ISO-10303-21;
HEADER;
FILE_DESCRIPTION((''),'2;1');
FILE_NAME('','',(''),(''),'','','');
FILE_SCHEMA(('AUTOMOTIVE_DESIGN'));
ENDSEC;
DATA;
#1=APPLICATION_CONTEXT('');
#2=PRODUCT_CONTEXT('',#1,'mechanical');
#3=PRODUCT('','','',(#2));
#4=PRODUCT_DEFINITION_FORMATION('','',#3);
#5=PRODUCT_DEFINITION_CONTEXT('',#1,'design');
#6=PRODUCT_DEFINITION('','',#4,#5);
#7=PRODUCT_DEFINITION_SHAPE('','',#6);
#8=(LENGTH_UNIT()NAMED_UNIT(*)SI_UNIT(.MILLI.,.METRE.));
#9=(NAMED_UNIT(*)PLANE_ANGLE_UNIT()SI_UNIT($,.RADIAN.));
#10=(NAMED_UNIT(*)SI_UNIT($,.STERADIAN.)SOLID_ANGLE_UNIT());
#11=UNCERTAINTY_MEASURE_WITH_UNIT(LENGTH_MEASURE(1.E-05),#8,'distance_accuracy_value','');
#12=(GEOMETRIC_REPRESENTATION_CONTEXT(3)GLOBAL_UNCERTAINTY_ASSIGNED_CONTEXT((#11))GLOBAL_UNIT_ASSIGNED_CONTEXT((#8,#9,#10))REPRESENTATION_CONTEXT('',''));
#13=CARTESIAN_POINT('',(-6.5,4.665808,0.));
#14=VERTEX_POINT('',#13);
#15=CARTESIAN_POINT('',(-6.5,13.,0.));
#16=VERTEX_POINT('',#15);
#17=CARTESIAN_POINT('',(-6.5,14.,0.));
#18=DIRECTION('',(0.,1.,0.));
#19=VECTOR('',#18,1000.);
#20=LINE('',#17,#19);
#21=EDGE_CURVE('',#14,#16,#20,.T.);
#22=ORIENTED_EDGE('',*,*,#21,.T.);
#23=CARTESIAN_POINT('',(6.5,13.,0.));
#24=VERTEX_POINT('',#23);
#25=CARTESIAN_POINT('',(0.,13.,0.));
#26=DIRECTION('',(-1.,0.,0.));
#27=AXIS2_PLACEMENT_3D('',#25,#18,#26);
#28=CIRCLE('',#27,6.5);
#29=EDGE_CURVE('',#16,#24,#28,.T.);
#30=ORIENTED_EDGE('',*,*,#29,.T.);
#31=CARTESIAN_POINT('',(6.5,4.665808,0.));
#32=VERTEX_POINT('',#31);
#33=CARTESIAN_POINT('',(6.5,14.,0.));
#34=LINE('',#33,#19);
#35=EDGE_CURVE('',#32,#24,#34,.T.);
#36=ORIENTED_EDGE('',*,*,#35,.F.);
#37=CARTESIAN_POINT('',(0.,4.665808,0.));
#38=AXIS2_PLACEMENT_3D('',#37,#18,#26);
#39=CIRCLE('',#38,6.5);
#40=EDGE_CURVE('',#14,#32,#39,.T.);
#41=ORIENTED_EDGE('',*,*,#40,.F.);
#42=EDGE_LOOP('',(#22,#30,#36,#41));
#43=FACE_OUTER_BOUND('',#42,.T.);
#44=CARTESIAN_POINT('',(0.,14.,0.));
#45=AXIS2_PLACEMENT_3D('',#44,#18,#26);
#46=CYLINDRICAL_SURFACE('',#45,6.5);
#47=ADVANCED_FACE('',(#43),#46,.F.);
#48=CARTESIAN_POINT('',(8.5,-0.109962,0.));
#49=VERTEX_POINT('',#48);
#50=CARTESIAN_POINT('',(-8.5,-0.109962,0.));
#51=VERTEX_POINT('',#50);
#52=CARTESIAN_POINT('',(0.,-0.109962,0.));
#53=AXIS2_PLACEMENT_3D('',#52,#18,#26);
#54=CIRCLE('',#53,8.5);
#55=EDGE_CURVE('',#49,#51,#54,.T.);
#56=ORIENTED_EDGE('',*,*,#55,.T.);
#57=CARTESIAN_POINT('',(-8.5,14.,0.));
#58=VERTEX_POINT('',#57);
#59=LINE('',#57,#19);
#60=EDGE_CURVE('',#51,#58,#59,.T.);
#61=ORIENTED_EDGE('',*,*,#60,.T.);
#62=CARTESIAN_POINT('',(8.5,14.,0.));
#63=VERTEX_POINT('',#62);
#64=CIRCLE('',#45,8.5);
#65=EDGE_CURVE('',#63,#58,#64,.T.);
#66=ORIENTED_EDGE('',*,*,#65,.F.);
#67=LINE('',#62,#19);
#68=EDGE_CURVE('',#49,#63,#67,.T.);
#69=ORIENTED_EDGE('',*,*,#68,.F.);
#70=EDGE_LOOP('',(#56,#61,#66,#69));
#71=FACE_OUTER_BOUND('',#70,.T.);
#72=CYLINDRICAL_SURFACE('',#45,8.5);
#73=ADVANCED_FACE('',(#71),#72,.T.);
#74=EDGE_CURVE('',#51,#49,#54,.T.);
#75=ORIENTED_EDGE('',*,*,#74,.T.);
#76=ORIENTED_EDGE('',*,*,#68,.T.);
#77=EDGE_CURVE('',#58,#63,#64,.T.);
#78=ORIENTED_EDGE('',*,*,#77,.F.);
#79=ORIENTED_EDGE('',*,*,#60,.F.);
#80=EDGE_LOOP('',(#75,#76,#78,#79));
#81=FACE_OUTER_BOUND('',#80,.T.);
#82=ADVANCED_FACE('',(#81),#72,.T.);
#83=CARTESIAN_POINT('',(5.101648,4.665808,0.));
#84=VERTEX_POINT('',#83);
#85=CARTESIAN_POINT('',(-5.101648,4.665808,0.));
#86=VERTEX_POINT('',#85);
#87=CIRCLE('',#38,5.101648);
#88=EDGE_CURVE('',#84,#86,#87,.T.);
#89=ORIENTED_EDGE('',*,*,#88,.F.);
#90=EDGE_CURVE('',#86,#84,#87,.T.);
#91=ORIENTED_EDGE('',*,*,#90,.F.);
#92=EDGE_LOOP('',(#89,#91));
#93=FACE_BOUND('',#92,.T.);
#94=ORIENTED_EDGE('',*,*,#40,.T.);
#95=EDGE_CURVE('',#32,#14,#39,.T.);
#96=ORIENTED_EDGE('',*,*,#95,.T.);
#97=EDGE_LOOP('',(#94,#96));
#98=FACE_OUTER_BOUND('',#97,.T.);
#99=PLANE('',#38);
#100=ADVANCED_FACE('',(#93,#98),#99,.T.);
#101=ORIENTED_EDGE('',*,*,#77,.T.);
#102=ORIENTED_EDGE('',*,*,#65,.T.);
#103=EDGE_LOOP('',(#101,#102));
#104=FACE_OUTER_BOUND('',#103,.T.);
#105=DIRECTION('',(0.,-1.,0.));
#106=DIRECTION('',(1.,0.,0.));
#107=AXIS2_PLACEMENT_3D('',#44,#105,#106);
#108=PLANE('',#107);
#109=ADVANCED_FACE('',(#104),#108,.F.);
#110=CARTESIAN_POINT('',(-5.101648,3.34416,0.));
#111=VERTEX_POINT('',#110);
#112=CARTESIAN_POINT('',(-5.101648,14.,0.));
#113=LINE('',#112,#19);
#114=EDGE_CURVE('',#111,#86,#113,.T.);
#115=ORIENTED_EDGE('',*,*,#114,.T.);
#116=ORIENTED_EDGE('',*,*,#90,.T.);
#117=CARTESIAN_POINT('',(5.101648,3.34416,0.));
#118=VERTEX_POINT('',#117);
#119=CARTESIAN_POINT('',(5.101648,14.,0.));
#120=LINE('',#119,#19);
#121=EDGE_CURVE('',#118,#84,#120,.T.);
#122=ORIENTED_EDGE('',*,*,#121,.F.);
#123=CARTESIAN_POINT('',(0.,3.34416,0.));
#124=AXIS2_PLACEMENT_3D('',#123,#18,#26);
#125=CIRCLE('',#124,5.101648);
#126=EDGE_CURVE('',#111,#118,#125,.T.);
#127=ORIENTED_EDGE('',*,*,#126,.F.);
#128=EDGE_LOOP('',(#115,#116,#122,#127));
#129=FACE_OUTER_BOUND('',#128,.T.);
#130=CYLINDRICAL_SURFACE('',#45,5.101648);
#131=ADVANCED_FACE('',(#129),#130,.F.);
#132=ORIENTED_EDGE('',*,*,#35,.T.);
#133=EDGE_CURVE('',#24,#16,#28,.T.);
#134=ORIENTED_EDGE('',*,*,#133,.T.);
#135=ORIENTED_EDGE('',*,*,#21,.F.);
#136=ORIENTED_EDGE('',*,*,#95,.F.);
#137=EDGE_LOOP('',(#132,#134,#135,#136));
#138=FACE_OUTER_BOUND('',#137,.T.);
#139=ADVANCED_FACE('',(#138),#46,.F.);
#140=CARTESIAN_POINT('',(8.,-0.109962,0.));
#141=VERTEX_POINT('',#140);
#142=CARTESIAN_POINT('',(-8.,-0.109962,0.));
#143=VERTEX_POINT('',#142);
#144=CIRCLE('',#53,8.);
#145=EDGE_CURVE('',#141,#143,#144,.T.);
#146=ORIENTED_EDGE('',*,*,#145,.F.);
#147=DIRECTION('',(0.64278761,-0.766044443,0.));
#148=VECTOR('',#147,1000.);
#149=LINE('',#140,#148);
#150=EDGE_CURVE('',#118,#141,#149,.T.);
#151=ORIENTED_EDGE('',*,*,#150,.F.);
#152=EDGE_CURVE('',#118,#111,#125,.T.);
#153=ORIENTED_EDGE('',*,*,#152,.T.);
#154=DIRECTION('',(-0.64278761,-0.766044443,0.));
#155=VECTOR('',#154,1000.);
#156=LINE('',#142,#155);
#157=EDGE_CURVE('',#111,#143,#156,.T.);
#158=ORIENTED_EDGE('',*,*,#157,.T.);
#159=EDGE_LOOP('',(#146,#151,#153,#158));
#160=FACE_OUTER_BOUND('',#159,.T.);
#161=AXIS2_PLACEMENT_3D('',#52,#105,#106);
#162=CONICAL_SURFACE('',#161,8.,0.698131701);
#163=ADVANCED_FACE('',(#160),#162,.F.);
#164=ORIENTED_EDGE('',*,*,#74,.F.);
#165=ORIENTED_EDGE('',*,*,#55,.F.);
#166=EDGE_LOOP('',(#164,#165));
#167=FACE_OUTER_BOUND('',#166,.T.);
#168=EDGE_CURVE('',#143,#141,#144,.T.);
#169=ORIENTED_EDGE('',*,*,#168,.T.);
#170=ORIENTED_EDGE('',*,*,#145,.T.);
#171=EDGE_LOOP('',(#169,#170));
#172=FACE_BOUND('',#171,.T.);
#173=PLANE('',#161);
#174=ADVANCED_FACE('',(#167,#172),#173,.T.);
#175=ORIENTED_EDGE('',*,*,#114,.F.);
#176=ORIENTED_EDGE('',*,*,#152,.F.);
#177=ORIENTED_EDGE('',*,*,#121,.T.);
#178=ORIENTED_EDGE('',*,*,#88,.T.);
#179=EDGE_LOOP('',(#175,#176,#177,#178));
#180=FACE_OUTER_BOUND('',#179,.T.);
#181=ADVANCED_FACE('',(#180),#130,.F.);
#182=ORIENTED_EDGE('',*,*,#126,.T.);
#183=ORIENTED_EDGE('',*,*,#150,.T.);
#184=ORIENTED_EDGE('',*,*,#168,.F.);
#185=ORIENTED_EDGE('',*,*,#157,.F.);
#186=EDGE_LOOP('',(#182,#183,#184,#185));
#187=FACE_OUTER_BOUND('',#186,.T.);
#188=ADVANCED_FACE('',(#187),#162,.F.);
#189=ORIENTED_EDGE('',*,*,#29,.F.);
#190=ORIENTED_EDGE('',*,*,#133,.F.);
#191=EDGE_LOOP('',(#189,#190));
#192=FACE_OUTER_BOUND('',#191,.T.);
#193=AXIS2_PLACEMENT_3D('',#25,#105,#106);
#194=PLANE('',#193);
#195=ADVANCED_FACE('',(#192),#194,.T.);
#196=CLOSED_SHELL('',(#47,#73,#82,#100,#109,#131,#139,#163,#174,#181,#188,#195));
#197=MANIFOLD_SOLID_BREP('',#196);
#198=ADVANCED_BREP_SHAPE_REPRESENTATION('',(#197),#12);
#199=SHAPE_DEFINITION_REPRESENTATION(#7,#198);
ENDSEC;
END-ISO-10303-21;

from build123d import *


with BuildPart() as part:
    # Sketch2 → Revolve1 (revolve)
    with BuildSketch(Plane.XY):
        Polygon((-8.5, 14), (-8.5, -0.10996164), (-8, -0.10996164), (-5.101647841, 3.344159959), (-5.101647841, 4.665808374), (-6.5, 4.665808374), (-6.5, 13), (0, 13), (0, 14), align=None)
    revolve(axis=Axis((0, 14, 0), (0, -1, 0)))


solid = part.part
